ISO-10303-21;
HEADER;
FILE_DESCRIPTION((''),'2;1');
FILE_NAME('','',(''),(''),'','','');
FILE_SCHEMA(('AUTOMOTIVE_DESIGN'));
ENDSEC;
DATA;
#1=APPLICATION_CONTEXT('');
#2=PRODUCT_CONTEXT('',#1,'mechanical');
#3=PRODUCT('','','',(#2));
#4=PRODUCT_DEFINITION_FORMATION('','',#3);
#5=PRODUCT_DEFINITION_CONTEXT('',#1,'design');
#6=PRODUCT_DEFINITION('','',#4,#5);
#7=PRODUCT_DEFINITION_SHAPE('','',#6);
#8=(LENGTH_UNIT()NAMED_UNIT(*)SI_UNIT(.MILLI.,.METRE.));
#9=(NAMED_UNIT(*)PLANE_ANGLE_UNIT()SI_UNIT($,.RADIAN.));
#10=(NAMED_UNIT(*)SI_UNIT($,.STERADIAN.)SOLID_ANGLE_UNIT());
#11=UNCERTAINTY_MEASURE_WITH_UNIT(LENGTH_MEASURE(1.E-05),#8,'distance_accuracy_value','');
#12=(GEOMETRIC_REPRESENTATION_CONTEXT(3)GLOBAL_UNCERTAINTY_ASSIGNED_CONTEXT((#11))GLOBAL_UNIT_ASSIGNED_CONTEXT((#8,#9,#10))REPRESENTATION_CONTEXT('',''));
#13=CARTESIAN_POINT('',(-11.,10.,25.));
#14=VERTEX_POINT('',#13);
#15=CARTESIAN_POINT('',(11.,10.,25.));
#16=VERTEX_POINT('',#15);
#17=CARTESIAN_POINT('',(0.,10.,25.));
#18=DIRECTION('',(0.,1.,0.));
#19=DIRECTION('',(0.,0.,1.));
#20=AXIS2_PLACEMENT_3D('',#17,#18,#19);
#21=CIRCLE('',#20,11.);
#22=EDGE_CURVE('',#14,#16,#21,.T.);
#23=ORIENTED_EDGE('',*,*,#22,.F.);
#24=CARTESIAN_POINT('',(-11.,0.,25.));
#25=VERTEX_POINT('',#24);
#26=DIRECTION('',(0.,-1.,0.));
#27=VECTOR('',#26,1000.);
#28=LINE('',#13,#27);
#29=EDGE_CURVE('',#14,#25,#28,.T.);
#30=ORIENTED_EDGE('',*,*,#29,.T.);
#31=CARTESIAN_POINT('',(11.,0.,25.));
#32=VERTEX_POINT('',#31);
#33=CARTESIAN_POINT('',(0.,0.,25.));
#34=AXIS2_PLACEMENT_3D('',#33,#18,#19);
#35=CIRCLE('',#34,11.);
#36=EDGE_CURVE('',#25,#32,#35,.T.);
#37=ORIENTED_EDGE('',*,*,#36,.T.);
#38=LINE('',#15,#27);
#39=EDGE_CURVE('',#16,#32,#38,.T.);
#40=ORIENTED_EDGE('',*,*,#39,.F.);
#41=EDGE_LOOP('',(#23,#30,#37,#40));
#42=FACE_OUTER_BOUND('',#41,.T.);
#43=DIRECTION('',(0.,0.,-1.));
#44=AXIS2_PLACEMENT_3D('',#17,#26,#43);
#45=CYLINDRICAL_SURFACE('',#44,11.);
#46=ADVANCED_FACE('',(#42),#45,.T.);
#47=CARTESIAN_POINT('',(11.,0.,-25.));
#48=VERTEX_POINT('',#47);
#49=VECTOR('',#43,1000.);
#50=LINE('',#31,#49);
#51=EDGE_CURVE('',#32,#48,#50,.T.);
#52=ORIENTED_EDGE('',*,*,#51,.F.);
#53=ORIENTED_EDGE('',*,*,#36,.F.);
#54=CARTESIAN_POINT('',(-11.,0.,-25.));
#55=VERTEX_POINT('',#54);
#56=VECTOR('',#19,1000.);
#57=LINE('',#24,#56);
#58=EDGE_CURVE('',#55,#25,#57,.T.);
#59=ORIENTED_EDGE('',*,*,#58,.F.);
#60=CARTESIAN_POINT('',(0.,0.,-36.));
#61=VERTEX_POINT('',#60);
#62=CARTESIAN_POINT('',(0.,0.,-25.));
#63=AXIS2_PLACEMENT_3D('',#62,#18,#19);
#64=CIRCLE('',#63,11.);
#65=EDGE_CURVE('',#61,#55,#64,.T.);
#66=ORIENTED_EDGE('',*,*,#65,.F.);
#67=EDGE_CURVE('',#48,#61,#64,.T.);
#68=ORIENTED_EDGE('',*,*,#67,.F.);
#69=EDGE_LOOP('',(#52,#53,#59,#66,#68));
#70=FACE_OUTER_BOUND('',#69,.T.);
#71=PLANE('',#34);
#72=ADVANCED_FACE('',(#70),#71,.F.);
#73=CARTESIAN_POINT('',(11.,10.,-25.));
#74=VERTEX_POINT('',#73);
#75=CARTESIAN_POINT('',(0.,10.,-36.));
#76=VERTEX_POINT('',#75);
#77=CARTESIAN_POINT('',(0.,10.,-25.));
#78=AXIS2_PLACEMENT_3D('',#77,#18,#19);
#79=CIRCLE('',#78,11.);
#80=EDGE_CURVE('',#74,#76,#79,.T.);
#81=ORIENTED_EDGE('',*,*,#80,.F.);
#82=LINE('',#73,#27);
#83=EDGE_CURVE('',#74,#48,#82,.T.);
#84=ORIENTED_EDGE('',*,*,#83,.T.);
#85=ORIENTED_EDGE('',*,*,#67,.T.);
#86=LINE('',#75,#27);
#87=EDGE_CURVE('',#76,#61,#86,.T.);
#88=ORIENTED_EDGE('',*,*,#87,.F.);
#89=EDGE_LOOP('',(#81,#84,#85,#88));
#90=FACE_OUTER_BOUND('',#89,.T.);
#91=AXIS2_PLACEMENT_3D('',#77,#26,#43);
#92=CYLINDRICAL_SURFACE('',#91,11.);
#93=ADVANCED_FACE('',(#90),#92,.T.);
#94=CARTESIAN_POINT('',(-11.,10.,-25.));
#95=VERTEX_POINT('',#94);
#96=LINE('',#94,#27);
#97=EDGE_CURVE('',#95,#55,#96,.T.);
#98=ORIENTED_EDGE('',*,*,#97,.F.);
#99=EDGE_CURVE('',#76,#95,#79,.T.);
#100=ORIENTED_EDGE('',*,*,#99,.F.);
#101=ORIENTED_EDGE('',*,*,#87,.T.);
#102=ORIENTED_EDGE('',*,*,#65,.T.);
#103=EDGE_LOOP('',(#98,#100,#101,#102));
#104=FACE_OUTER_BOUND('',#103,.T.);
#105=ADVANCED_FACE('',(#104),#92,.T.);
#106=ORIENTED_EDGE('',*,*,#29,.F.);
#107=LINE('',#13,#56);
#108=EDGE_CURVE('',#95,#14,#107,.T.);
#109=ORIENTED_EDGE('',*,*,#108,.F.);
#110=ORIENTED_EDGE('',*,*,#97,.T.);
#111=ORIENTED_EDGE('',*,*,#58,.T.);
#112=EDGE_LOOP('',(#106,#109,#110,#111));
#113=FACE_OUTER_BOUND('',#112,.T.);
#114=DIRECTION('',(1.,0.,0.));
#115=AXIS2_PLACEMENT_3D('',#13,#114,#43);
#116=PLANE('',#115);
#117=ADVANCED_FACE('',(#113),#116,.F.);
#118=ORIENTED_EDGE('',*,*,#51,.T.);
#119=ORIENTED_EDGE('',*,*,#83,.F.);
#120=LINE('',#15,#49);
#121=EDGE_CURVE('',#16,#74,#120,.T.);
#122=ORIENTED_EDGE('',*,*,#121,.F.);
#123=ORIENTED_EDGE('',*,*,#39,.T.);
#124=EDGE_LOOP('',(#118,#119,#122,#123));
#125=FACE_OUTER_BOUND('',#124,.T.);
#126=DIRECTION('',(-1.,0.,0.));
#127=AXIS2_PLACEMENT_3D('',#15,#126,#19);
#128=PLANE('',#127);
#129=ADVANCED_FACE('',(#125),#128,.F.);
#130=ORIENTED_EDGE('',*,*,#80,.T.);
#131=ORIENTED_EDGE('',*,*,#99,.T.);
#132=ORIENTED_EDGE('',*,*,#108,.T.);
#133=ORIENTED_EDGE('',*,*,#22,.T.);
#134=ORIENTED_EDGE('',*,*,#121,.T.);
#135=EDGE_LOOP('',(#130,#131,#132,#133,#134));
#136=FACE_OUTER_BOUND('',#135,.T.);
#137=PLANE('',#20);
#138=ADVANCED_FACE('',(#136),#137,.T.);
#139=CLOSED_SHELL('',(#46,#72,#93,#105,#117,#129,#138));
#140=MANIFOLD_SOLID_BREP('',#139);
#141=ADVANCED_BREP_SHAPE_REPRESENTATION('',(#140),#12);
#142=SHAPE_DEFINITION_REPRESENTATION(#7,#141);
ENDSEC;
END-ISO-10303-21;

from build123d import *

# Parameters (mm, degrees)
BOSS_EXTRUDE1_DEPTH = 10


with BuildPart() as part:
    # Sketch1 → Boss-Extrude1 (new body)
    with BuildSketch(Plane(origin=(0, 0, 0), x_dir=(1, 0, 0), z_dir=(0, 1, 0))):
        with BuildLine():
            Line((-11, -25), (-11, 25))
            ThreePointArc((-11, 25), (0, 36), (11, 25))
            Line((11, 25), (11, -25))
            ThreePointArc((11, -25), (0, -36), (-11, -25))
        make_face()
    extrude(amount=BOSS_EXTRUDE1_DEPTH)


solid = part.part
